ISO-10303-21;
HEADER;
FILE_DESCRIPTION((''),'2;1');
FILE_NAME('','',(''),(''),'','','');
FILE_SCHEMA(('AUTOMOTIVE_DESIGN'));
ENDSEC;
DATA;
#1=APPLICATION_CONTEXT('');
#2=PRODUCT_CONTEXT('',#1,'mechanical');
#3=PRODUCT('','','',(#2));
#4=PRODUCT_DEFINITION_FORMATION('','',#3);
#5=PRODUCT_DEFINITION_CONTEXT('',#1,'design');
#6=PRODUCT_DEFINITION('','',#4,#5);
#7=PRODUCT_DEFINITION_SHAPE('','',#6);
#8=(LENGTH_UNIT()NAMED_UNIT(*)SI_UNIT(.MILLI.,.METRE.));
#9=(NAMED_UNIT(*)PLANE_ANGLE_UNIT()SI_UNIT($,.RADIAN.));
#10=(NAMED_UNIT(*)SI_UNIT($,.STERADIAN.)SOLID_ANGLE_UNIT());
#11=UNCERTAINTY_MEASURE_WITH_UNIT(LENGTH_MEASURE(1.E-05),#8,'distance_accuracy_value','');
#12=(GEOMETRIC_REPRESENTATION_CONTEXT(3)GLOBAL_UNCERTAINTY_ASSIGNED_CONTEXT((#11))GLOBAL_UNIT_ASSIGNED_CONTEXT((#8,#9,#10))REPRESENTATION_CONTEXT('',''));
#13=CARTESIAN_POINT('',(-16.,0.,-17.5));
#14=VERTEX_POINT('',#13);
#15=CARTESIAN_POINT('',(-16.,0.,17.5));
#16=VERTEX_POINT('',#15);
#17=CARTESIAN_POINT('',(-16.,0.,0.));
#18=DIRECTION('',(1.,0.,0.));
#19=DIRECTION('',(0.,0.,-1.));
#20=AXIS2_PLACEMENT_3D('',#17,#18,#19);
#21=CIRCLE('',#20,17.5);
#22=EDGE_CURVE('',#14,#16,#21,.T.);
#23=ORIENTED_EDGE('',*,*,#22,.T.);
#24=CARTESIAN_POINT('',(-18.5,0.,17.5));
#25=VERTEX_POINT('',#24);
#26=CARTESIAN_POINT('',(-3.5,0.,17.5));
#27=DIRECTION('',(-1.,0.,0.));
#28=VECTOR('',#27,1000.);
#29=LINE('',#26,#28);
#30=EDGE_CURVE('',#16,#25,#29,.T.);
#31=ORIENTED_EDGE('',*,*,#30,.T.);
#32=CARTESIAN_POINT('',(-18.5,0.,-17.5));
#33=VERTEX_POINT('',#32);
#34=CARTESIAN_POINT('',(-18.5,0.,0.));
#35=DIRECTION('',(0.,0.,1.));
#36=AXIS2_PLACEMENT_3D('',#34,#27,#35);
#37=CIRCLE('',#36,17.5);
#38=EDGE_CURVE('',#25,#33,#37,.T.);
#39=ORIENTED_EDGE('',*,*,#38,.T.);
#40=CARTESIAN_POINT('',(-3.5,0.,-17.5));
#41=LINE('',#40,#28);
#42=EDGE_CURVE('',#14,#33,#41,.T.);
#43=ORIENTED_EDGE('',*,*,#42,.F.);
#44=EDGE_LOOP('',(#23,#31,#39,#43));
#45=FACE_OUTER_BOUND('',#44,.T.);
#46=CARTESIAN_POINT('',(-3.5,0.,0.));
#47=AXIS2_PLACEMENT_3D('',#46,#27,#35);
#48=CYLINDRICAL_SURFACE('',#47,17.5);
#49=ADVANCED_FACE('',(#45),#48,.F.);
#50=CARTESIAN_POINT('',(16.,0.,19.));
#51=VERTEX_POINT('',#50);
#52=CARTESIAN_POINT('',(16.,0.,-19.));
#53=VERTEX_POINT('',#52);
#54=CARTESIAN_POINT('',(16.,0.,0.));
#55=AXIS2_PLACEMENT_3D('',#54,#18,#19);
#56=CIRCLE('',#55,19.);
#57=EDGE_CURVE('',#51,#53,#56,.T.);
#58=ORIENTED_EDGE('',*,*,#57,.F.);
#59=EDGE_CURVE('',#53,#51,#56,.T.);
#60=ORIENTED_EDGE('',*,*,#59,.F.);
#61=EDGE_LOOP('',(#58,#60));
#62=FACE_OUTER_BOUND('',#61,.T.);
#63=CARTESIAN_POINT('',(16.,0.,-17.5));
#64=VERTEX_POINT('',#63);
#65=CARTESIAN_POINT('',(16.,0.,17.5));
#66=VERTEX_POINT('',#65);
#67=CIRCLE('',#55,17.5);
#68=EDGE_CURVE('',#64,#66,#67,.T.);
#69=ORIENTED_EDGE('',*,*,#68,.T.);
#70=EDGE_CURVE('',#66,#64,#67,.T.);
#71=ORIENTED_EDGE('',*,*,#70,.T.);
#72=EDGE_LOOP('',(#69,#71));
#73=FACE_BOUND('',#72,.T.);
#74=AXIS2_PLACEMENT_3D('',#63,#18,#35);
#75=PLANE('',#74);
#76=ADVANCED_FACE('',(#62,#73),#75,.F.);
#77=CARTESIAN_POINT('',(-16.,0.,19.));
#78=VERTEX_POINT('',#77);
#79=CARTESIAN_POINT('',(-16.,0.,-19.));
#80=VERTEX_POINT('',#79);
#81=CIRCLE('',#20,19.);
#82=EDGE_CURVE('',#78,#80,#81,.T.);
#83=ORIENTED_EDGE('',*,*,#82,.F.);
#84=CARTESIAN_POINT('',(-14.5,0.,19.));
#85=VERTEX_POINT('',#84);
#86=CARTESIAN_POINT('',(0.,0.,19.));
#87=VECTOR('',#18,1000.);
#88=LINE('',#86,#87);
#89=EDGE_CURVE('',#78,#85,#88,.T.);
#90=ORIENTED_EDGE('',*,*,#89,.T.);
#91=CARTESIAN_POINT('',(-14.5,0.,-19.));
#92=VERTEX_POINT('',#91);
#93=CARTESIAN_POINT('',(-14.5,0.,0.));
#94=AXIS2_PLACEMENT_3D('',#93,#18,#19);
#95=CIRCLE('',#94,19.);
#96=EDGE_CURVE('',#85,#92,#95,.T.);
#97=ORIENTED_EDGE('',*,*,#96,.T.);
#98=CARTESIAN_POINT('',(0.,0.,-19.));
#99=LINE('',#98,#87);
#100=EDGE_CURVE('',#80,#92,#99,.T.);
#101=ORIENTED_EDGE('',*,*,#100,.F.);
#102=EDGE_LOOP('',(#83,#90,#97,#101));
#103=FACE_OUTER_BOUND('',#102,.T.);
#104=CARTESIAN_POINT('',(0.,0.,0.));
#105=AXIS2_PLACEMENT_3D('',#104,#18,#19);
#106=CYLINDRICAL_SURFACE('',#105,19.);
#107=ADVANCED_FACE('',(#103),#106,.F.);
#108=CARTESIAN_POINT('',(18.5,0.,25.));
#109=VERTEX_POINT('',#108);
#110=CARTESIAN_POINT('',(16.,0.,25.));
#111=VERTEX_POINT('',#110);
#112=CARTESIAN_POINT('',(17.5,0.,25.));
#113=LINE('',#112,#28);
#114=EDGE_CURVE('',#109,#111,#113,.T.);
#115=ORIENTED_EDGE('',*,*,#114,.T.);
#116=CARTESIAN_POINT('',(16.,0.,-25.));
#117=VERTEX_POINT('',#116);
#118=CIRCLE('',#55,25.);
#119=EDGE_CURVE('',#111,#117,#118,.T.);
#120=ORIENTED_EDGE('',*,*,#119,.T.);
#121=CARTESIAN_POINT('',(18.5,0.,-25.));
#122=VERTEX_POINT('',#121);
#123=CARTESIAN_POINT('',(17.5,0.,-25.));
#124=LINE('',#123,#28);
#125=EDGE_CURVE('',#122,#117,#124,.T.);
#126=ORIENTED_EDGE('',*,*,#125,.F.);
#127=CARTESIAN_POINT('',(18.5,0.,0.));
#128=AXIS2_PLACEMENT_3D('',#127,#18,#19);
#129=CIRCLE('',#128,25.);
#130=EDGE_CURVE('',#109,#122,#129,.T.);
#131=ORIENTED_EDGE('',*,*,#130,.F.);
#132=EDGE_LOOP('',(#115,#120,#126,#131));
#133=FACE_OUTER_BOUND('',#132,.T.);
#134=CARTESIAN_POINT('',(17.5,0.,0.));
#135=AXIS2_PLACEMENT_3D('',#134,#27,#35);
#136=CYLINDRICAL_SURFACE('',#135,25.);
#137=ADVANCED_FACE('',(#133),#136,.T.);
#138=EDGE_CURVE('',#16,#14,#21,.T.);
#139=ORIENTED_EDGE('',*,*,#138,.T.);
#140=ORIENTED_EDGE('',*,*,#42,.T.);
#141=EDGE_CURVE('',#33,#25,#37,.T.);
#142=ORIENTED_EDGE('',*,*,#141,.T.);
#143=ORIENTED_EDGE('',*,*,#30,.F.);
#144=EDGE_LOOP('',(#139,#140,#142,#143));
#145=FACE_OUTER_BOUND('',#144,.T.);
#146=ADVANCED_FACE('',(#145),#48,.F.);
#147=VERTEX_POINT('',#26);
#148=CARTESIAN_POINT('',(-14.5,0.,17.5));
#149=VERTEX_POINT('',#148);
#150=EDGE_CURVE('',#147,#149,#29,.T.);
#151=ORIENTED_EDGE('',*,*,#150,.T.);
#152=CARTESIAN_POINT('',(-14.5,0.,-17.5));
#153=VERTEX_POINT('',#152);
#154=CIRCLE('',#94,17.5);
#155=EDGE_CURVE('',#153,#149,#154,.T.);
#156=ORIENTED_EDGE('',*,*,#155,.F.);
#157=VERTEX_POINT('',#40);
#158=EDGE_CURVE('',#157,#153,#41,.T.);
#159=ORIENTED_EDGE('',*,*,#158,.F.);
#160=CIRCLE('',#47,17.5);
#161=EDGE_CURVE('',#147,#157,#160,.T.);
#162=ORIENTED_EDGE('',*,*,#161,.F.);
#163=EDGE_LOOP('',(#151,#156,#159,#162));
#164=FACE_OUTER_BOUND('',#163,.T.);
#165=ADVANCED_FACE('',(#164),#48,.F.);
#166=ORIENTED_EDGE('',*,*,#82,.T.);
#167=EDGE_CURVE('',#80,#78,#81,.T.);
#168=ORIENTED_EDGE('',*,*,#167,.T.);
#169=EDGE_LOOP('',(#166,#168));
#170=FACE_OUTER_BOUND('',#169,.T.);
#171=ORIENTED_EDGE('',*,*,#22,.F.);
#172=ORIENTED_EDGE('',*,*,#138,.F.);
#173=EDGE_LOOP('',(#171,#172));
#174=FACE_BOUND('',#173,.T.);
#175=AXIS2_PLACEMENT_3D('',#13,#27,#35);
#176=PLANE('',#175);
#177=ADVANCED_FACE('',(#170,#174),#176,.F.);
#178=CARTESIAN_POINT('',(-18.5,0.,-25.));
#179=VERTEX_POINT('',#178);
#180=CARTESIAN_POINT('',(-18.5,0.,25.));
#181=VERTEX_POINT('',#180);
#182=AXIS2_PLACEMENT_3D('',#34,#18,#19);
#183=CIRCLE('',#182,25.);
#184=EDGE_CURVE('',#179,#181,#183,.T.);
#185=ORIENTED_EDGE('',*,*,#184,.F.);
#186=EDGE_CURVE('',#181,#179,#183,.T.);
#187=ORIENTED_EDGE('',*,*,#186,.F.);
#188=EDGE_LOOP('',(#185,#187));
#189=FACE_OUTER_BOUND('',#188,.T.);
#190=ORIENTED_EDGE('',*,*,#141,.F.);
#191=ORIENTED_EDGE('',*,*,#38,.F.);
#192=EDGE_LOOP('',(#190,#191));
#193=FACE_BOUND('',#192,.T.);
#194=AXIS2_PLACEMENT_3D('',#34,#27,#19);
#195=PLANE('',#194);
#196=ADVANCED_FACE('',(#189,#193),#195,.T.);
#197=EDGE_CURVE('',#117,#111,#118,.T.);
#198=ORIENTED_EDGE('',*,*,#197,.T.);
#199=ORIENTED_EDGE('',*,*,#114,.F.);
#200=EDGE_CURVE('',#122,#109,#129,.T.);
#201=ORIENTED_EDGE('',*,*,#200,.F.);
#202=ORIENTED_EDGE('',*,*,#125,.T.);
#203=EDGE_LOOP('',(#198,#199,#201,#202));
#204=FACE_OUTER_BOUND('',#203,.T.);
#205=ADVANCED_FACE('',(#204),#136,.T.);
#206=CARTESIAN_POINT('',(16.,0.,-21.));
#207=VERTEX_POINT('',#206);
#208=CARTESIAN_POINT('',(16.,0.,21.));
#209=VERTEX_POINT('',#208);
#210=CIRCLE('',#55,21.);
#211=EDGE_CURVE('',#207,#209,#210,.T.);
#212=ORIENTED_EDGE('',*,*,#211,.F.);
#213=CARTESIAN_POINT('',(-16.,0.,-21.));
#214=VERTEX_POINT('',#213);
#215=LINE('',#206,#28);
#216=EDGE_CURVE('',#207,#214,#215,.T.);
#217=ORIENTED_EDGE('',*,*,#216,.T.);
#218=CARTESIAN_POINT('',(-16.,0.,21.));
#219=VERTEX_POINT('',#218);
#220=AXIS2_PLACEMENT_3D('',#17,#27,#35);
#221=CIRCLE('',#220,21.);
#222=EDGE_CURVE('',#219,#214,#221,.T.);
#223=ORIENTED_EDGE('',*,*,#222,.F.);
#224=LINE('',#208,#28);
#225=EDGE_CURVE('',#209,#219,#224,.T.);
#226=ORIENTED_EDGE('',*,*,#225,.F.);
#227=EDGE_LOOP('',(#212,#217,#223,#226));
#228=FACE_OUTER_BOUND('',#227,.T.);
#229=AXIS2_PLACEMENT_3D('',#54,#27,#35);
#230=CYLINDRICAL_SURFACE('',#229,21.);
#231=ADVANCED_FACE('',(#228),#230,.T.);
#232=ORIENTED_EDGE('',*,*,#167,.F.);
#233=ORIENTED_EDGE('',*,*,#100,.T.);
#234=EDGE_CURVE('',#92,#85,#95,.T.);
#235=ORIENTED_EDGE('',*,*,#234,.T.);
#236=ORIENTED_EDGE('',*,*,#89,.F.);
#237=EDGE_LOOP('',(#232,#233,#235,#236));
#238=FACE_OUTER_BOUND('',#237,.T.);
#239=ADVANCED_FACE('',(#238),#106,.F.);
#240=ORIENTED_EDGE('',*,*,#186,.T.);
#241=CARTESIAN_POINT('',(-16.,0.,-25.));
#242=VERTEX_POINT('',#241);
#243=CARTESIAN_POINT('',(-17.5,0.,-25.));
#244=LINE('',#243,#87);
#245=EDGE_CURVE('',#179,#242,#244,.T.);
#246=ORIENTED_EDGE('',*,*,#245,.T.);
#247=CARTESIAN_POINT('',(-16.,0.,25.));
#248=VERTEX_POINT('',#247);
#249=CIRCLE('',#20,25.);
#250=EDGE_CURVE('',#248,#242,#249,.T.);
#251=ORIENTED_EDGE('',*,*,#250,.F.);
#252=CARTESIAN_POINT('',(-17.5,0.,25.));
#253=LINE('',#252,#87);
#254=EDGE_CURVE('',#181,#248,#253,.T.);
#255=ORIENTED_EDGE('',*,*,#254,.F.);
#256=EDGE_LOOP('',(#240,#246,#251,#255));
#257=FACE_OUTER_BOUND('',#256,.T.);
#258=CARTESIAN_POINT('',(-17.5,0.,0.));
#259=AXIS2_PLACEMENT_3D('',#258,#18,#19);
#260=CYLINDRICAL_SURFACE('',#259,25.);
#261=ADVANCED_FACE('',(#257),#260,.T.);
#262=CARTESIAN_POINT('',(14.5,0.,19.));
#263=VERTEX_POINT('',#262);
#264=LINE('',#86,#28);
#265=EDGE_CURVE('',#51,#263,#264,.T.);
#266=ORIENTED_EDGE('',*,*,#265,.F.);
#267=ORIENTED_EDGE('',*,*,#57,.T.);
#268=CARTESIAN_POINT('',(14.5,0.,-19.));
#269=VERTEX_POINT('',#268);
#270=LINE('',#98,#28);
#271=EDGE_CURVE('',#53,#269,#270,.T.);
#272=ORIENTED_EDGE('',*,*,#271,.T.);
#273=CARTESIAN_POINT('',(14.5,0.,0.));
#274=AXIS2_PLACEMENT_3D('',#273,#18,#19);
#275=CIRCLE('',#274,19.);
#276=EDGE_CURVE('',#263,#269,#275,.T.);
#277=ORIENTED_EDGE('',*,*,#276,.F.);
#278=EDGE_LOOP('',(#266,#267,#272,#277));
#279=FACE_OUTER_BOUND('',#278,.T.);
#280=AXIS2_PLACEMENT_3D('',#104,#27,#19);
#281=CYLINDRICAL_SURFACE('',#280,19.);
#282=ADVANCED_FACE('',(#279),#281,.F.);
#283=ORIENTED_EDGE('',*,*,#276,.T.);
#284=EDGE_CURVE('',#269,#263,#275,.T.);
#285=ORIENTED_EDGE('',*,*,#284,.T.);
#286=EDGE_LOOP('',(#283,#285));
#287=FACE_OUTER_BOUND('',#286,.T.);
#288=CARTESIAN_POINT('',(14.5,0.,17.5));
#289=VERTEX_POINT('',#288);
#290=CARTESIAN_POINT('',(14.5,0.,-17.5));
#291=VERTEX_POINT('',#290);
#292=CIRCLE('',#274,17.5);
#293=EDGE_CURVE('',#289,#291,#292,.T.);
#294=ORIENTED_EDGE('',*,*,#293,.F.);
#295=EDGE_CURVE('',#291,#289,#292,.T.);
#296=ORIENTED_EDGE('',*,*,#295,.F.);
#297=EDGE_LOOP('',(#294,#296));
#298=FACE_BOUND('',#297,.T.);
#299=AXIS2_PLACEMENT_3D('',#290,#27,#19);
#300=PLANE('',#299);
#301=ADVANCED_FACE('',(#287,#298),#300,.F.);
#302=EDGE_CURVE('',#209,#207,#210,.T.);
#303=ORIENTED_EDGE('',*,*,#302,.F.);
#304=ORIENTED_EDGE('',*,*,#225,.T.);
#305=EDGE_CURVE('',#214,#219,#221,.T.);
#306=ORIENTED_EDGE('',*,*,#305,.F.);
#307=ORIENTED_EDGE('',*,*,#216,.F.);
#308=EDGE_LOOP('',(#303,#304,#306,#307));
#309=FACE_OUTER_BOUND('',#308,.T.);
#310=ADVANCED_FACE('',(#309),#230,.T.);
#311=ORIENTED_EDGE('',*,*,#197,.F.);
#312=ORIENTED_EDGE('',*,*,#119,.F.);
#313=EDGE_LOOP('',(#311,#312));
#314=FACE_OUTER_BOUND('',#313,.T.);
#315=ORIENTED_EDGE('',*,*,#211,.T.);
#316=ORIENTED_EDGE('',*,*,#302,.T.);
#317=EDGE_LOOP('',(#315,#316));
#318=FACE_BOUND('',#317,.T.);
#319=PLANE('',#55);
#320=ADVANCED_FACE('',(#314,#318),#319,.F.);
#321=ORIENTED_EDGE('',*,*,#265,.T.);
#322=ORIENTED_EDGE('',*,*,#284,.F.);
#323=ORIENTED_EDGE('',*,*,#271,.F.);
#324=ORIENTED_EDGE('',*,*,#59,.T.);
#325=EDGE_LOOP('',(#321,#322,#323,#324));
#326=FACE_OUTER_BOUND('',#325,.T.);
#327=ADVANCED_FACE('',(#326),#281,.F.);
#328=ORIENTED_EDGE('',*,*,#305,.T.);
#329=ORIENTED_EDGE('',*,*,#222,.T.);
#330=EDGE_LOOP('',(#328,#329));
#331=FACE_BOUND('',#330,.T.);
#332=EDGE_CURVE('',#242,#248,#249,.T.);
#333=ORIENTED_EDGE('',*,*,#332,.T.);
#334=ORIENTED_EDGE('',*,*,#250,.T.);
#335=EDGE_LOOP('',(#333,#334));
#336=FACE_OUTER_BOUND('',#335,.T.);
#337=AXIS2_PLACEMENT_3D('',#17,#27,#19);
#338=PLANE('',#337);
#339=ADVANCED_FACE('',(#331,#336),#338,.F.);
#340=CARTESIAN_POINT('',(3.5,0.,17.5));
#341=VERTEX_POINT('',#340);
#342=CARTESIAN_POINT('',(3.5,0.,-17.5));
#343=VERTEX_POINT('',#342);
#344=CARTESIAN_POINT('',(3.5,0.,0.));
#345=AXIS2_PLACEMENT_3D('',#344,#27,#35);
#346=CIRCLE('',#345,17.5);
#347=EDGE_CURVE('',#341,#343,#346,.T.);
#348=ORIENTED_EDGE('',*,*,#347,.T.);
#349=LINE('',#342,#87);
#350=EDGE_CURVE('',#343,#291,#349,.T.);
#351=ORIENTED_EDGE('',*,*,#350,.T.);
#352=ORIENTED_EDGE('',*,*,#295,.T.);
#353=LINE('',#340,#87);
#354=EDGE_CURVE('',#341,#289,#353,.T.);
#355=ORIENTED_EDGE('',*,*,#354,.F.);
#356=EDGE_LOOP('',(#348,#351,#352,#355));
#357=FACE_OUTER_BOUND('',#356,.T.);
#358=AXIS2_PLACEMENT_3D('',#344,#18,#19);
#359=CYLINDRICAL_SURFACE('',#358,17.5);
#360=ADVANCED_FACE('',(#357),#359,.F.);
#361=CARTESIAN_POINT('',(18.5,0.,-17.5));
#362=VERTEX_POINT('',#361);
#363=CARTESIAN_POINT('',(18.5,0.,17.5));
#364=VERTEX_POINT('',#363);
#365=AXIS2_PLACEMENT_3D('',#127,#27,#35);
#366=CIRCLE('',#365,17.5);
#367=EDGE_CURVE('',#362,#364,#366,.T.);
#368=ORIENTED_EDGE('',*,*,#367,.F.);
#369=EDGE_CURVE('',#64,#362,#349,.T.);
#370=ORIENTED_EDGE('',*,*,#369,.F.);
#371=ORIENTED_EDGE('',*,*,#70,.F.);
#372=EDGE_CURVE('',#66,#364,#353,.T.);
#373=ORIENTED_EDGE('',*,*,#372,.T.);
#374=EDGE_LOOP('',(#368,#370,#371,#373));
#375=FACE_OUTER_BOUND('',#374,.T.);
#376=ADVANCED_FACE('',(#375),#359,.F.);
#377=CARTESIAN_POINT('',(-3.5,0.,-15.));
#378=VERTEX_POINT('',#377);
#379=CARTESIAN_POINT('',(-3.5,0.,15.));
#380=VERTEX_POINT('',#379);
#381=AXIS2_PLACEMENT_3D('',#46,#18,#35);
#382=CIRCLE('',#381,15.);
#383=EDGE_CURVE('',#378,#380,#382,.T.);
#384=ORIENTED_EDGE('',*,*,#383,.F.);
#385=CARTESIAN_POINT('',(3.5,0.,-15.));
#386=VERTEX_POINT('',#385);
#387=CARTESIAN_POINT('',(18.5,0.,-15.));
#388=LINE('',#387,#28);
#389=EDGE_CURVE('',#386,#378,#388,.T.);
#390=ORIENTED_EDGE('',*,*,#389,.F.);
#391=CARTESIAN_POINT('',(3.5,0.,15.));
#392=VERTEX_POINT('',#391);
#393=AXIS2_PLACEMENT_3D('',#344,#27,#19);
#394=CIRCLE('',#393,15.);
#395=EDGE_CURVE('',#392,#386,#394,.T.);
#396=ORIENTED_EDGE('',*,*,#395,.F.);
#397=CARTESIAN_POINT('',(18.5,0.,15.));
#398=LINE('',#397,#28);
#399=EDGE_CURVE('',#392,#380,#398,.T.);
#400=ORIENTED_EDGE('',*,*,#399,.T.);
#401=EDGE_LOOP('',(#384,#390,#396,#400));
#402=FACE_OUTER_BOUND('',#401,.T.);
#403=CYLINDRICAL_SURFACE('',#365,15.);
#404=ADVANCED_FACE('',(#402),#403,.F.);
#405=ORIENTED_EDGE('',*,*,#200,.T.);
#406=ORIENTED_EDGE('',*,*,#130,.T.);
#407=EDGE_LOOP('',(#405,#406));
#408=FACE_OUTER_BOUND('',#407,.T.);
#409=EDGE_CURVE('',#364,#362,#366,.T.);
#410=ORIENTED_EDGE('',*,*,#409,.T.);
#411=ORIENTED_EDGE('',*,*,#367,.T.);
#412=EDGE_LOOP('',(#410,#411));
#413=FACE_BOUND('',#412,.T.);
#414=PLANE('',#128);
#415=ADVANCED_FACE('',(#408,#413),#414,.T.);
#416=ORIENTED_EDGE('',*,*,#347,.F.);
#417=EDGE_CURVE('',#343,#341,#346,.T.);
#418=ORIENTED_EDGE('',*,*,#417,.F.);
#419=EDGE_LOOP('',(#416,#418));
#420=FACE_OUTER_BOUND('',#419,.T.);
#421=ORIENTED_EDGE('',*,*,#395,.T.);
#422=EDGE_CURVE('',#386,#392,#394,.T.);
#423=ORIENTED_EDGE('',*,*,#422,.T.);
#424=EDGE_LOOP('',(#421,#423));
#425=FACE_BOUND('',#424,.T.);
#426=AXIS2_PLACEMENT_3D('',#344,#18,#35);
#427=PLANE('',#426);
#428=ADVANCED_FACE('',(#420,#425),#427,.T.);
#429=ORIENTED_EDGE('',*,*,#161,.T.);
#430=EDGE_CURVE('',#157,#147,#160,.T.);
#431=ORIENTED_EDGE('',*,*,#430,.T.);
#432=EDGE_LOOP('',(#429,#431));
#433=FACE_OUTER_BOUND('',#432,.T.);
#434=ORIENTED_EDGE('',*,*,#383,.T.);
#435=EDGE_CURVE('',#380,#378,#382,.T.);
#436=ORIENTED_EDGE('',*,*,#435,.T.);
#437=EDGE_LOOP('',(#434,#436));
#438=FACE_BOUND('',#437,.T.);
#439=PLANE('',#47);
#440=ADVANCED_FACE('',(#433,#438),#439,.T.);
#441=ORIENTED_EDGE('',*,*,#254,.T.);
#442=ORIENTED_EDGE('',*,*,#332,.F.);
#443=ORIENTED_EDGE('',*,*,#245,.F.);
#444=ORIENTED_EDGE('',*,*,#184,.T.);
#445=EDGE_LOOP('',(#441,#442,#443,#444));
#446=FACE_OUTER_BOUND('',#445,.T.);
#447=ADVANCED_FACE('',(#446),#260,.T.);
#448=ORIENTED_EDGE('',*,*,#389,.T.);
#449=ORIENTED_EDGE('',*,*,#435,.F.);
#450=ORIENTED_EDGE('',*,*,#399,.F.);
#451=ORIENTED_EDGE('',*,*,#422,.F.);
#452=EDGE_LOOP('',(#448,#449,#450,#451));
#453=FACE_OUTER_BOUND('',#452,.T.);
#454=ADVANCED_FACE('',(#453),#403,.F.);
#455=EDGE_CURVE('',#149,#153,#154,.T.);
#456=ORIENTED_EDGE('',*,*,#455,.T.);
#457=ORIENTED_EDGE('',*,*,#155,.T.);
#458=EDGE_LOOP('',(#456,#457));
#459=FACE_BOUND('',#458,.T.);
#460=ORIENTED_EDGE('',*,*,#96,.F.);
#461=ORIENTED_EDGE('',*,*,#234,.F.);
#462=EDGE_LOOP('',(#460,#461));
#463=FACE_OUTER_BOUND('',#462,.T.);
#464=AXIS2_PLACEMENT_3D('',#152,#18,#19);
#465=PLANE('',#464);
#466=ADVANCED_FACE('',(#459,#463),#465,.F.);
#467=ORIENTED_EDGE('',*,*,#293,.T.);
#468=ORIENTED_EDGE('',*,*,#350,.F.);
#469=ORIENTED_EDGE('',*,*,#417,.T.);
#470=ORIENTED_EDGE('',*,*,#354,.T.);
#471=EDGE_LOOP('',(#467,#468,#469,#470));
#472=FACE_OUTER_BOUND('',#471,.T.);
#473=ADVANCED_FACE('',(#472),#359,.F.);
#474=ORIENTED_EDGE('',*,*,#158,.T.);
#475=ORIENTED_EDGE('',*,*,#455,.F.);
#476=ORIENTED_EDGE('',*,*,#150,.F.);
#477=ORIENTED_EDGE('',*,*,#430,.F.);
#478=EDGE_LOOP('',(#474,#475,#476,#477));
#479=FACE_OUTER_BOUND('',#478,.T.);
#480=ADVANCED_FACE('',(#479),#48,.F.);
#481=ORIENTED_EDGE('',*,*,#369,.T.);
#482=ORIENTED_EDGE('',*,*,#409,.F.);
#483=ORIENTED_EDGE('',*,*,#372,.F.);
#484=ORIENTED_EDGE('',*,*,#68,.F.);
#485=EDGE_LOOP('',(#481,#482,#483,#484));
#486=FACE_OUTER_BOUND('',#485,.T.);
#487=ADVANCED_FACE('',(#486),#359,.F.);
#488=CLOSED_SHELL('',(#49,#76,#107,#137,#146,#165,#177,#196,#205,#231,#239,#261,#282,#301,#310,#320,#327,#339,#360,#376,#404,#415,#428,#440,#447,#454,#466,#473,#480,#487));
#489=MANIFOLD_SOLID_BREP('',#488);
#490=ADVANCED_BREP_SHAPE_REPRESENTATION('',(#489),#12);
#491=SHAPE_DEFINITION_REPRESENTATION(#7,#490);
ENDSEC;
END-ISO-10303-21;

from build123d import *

# Parameters (mm, degrees)
SKETCH_1_R          = 21
EXTRUDE_1_DEPTH     = 16
SKETCH_6_R          = 25
EXTRUDE_2_DEPTH     = 1.5
SKETCH_7_R          = 25
EXTRUDE_3_DEPTH     = 1
SKETCH_8_R          = 15
CUT_EXTRUDE_1_DEPTH = 52.176166328
SKETCH_9_R          = 17.5
CUT_EXTRUDE_2_DEPTH = 15
SKETCH_10_W         = 1.5
SKETCH_10_H         = 1.5


with BuildPart() as part:
    # 草图1 → 拉伸1 (new, symmetric)
    with BuildSketch(Plane(origin=(0, 0, 0), x_dir=(0, 0, -1), z_dir=(1, 0, 0))):
        Circle(SKETCH_1_R)
    extrude(amount=EXTRUDE_1_DEPTH, both=True)

    # 草图6 → 凸台-拉伸2 (add)
    with BuildSketch(Plane(origin=(16, 0, 0), x_dir=(0, 0, -1), z_dir=(1, 0, 0))):
        Circle(SKETCH_6_R)
    extrude_2 = extrude(amount=EXTRUDE_2_DEPTH)

    # 草图7 → 凸台-拉伸3 (add)
    with BuildSketch(Plane(origin=(17.5, 0, 0), x_dir=(0, 0, -1), z_dir=(1, 0, 0))):
        Circle(SKETCH_7_R)
    extrude_3 = extrude(amount=EXTRUDE_3_DEPTH)

    # 镜向2: 凸台-拉伸2, 凸台-拉伸3 across plane
    add(extrude_2.mirror(Plane(origin=(0, 0, 0), x_dir=(0, 0, 1), z_dir=(1, 0, 0))))
    add(extrude_3.mirror(Plane(origin=(0, 0, 0), x_dir=(0, 0, 1), z_dir=(1, 0, 0))))

    # 草图8 → 切除-拉伸1 (cut, through all)
    with BuildSketch(Plane.ZY.offset(18.5)):
        Circle(SKETCH_8_R)
    extrude(amount=-CUT_EXTRUDE_1_DEPTH, mode=Mode.SUBTRACT)

    # 草图9 → Cut-Extrude 2 (cut)
    with BuildSketch(Plane.ZY.offset(18.5)):
        Circle(SKETCH_9_R)
    cut_extrude_2 = extrude(amount=-CUT_EXTRUDE_2_DEPTH, mode=Mode.SUBTRACT)

    # 草图10 → 切除-旋转1 (revolve, cut)
    with BuildSketch(Plane(origin=(0, 0, 0), x_dir=(1, 0, 0), z_dir=(0, 1, 0)), mode=Mode.PRIVATE) as cut_revolve_1_sk:
        with Locations((-15.25, 18.25)):
            Rectangle(SKETCH_10_W, SKETCH_10_H)
    cut_revolve_1 = revolve(cut_revolve_1_sk.sketch.rotate(Axis((0, 0, 0), (-1, 0, 0)), 180), axis=Axis((0, 0, 0), (-1, 0, 0)), mode=Mode.SUBTRACT)

    # 镜向3: Cut-Extrude 2, 切除-旋转1 across plane
    add(cut_extrude_2.mirror(Plane(origin=(0, 0, 0), x_dir=(0, 0, 1), z_dir=(1, 0, 0))), mode=Mode.SUBTRACT)
    add(cut_revolve_1.mirror(Plane(origin=(0, 0, 0), x_dir=(0, 0, 1), z_dir=(1, 0, 0))), mode=Mode.SUBTRACT)


solid = part.part
